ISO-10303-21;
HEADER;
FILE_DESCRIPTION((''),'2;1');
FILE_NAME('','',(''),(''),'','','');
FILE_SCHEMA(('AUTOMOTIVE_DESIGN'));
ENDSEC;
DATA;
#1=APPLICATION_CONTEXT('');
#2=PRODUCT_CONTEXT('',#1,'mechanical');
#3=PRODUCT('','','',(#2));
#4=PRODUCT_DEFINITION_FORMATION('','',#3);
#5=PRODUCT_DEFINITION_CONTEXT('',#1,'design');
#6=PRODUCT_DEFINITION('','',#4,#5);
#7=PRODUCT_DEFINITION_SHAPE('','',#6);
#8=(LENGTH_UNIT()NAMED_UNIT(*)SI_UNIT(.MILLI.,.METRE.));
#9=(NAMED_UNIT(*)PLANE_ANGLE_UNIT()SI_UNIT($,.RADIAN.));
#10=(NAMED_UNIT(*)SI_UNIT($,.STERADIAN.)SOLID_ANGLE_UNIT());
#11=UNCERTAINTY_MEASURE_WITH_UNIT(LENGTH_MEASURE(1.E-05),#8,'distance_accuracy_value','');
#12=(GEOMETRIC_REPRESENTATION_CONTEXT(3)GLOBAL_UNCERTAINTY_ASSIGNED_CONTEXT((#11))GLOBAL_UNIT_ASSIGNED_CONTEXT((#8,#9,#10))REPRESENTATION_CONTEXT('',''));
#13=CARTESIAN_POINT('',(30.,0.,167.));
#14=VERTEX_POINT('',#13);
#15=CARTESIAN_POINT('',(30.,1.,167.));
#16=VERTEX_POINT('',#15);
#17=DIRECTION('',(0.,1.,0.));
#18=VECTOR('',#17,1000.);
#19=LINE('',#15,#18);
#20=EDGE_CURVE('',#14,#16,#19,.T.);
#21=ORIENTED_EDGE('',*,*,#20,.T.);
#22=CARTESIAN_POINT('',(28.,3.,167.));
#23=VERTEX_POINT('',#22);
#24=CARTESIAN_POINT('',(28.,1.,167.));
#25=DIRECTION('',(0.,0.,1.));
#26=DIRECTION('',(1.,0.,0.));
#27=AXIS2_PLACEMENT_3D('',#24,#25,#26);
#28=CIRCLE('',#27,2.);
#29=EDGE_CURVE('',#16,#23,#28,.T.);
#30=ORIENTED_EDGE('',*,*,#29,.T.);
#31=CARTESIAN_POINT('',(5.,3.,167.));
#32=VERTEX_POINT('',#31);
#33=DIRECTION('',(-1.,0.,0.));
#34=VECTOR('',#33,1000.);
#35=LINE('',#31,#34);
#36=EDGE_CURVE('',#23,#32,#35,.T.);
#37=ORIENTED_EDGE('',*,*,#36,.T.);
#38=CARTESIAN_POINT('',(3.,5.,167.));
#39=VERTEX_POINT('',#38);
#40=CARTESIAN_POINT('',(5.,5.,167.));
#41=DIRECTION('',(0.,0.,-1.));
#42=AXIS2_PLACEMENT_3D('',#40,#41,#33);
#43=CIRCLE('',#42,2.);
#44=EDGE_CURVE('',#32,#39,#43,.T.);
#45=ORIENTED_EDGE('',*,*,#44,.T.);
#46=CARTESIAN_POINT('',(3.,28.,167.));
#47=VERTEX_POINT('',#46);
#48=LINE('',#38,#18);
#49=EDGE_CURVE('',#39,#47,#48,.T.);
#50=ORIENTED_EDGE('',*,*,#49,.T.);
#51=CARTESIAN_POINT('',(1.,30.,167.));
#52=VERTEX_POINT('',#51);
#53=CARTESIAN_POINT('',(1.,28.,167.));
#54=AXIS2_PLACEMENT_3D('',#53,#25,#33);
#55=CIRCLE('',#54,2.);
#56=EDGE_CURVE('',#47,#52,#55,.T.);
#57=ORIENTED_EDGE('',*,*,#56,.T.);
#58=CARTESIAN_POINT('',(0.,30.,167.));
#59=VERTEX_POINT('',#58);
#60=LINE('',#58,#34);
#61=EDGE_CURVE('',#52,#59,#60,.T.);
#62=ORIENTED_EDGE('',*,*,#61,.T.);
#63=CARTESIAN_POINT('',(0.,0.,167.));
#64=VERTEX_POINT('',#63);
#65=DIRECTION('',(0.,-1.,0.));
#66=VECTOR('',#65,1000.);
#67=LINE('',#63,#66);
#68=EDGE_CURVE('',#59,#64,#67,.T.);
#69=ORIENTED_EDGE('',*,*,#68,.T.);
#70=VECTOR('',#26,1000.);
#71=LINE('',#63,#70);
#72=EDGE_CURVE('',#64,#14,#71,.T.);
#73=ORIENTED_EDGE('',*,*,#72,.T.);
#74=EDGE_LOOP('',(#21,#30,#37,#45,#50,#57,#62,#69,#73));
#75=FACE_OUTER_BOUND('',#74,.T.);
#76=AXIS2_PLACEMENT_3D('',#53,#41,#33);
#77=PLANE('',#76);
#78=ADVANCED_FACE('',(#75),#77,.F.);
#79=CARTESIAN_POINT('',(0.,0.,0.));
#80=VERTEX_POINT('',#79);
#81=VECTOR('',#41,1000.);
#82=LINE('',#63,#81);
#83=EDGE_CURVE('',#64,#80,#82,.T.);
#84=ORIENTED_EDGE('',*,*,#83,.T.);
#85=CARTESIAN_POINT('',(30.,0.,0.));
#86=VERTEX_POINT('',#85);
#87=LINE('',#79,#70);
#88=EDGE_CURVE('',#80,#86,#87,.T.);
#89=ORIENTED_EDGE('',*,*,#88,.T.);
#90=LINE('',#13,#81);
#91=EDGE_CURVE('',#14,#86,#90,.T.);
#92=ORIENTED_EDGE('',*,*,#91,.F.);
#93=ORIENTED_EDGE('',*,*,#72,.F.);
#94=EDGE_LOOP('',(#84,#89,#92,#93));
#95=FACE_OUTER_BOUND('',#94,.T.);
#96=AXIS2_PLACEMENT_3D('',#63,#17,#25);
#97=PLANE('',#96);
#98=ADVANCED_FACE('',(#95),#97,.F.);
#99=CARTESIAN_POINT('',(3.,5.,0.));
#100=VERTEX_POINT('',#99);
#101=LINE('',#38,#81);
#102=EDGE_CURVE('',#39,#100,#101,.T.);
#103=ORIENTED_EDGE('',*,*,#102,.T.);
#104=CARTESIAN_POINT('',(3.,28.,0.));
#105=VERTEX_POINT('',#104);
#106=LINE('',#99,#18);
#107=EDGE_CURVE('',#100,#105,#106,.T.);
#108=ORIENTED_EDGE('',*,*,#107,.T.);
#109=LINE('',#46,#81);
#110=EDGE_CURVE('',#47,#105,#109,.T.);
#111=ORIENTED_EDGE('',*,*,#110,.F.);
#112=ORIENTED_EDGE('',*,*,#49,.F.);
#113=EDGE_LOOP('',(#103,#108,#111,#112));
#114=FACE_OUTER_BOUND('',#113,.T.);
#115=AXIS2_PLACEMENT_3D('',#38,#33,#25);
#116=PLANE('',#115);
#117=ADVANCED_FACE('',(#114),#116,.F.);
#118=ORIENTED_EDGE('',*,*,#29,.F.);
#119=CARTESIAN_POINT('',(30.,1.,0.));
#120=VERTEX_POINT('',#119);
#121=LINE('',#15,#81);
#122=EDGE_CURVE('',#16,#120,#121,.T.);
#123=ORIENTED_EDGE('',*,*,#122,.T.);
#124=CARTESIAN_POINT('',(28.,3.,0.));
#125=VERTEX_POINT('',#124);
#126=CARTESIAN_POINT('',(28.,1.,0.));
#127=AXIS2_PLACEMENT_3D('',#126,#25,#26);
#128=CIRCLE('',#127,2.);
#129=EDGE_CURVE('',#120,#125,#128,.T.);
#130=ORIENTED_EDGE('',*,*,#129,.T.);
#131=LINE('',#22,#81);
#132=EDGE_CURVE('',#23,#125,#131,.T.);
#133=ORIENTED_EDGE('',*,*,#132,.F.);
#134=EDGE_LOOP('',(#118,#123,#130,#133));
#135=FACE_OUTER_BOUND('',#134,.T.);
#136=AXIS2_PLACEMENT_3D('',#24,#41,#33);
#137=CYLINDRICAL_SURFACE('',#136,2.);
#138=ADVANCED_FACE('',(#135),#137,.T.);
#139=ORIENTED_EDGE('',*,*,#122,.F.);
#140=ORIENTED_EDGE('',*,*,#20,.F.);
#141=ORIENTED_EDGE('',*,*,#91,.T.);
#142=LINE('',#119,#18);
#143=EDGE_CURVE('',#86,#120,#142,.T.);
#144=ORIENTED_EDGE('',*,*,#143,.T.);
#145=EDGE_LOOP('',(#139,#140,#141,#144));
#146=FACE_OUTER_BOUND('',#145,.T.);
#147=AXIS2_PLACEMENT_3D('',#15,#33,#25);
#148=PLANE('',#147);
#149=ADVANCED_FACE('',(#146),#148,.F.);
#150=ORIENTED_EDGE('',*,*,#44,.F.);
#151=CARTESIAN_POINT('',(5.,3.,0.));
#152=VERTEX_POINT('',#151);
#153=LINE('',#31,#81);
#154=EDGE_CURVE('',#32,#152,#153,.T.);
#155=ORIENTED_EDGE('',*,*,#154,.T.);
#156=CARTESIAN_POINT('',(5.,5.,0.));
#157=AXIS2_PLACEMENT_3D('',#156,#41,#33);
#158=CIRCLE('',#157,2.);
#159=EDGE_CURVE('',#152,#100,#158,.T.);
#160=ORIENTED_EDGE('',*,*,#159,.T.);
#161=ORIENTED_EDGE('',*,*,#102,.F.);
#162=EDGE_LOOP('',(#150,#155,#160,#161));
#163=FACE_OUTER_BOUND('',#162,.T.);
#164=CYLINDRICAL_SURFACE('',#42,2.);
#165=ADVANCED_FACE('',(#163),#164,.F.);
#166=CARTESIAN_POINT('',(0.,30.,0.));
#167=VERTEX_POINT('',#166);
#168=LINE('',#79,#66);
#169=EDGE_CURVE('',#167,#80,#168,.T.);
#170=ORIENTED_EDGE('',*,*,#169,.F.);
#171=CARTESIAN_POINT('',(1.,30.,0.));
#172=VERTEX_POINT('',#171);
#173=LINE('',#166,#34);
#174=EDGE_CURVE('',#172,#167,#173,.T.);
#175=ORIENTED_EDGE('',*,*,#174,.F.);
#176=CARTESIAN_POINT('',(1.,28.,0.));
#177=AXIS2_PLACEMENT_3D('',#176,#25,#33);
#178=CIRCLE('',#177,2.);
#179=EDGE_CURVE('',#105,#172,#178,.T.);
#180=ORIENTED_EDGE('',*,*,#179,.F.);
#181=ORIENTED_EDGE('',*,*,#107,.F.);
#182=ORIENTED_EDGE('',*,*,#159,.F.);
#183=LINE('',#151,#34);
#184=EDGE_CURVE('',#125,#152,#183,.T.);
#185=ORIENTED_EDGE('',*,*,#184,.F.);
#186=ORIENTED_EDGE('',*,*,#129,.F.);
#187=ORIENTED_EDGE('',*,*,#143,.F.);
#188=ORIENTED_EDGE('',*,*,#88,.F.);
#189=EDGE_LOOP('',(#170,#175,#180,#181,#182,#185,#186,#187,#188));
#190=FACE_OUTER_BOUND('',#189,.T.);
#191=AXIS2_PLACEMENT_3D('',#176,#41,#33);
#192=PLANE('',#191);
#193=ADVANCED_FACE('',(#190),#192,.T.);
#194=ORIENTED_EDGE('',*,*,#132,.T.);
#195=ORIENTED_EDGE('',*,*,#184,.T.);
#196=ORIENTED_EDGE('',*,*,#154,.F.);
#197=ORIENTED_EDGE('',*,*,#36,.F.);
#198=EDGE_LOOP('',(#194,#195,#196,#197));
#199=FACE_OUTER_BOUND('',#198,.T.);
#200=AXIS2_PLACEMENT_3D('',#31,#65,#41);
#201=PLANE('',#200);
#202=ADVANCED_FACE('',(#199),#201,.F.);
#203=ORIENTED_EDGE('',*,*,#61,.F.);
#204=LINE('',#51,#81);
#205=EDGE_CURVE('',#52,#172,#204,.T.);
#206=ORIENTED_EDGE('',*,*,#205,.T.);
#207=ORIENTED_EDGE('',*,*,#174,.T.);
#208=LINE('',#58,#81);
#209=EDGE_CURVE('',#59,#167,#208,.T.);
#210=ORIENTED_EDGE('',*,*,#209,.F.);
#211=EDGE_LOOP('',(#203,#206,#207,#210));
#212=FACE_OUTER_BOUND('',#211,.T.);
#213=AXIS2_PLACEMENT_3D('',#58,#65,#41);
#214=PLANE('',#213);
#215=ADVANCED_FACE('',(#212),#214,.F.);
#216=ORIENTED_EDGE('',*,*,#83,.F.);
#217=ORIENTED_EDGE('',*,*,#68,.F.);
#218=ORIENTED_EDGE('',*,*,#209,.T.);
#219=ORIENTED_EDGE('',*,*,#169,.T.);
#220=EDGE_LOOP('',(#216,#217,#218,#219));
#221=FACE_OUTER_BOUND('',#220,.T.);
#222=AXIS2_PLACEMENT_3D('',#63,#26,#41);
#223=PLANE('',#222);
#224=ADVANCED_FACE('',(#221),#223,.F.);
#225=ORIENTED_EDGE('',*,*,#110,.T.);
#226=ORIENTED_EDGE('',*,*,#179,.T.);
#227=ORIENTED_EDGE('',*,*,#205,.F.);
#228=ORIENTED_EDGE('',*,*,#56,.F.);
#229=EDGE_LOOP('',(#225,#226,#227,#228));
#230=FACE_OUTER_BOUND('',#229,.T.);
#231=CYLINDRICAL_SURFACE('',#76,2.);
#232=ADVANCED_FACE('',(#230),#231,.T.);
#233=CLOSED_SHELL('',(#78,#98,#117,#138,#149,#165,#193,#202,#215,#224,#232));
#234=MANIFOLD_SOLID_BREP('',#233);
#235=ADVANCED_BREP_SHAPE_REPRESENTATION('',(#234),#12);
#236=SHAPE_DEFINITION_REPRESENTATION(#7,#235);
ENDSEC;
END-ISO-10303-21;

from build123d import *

# Parameters (mm, degrees)
BOSS_EXTRUDE1_DEPTH = 167


with BuildPart() as part:
    # Sketch1 → Boss-Extrude1 (new body)
    with BuildSketch(Plane.XY):
        with BuildLine():
            Line((0, 0), (30, 0))
            Line((30, 0), (30, 1))
            ThreePointArc((30, 1), (29.414213562, 2.414213562), (28, 3))
            Line((28, 3), (5, 3))
            ThreePointArc((5, 3), (3.585786438, 3.585786438), (3, 5))
            Line((3, 5), (3, 28))
            ThreePointArc((3, 28), (2.414213562, 29.414213562), (1, 30))
            Line((1, 30), (0, 30))
            Line((0, 30), (0, 0))
        make_face()
    extrude(amount=BOSS_EXTRUDE1_DEPTH)


solid = part.part
